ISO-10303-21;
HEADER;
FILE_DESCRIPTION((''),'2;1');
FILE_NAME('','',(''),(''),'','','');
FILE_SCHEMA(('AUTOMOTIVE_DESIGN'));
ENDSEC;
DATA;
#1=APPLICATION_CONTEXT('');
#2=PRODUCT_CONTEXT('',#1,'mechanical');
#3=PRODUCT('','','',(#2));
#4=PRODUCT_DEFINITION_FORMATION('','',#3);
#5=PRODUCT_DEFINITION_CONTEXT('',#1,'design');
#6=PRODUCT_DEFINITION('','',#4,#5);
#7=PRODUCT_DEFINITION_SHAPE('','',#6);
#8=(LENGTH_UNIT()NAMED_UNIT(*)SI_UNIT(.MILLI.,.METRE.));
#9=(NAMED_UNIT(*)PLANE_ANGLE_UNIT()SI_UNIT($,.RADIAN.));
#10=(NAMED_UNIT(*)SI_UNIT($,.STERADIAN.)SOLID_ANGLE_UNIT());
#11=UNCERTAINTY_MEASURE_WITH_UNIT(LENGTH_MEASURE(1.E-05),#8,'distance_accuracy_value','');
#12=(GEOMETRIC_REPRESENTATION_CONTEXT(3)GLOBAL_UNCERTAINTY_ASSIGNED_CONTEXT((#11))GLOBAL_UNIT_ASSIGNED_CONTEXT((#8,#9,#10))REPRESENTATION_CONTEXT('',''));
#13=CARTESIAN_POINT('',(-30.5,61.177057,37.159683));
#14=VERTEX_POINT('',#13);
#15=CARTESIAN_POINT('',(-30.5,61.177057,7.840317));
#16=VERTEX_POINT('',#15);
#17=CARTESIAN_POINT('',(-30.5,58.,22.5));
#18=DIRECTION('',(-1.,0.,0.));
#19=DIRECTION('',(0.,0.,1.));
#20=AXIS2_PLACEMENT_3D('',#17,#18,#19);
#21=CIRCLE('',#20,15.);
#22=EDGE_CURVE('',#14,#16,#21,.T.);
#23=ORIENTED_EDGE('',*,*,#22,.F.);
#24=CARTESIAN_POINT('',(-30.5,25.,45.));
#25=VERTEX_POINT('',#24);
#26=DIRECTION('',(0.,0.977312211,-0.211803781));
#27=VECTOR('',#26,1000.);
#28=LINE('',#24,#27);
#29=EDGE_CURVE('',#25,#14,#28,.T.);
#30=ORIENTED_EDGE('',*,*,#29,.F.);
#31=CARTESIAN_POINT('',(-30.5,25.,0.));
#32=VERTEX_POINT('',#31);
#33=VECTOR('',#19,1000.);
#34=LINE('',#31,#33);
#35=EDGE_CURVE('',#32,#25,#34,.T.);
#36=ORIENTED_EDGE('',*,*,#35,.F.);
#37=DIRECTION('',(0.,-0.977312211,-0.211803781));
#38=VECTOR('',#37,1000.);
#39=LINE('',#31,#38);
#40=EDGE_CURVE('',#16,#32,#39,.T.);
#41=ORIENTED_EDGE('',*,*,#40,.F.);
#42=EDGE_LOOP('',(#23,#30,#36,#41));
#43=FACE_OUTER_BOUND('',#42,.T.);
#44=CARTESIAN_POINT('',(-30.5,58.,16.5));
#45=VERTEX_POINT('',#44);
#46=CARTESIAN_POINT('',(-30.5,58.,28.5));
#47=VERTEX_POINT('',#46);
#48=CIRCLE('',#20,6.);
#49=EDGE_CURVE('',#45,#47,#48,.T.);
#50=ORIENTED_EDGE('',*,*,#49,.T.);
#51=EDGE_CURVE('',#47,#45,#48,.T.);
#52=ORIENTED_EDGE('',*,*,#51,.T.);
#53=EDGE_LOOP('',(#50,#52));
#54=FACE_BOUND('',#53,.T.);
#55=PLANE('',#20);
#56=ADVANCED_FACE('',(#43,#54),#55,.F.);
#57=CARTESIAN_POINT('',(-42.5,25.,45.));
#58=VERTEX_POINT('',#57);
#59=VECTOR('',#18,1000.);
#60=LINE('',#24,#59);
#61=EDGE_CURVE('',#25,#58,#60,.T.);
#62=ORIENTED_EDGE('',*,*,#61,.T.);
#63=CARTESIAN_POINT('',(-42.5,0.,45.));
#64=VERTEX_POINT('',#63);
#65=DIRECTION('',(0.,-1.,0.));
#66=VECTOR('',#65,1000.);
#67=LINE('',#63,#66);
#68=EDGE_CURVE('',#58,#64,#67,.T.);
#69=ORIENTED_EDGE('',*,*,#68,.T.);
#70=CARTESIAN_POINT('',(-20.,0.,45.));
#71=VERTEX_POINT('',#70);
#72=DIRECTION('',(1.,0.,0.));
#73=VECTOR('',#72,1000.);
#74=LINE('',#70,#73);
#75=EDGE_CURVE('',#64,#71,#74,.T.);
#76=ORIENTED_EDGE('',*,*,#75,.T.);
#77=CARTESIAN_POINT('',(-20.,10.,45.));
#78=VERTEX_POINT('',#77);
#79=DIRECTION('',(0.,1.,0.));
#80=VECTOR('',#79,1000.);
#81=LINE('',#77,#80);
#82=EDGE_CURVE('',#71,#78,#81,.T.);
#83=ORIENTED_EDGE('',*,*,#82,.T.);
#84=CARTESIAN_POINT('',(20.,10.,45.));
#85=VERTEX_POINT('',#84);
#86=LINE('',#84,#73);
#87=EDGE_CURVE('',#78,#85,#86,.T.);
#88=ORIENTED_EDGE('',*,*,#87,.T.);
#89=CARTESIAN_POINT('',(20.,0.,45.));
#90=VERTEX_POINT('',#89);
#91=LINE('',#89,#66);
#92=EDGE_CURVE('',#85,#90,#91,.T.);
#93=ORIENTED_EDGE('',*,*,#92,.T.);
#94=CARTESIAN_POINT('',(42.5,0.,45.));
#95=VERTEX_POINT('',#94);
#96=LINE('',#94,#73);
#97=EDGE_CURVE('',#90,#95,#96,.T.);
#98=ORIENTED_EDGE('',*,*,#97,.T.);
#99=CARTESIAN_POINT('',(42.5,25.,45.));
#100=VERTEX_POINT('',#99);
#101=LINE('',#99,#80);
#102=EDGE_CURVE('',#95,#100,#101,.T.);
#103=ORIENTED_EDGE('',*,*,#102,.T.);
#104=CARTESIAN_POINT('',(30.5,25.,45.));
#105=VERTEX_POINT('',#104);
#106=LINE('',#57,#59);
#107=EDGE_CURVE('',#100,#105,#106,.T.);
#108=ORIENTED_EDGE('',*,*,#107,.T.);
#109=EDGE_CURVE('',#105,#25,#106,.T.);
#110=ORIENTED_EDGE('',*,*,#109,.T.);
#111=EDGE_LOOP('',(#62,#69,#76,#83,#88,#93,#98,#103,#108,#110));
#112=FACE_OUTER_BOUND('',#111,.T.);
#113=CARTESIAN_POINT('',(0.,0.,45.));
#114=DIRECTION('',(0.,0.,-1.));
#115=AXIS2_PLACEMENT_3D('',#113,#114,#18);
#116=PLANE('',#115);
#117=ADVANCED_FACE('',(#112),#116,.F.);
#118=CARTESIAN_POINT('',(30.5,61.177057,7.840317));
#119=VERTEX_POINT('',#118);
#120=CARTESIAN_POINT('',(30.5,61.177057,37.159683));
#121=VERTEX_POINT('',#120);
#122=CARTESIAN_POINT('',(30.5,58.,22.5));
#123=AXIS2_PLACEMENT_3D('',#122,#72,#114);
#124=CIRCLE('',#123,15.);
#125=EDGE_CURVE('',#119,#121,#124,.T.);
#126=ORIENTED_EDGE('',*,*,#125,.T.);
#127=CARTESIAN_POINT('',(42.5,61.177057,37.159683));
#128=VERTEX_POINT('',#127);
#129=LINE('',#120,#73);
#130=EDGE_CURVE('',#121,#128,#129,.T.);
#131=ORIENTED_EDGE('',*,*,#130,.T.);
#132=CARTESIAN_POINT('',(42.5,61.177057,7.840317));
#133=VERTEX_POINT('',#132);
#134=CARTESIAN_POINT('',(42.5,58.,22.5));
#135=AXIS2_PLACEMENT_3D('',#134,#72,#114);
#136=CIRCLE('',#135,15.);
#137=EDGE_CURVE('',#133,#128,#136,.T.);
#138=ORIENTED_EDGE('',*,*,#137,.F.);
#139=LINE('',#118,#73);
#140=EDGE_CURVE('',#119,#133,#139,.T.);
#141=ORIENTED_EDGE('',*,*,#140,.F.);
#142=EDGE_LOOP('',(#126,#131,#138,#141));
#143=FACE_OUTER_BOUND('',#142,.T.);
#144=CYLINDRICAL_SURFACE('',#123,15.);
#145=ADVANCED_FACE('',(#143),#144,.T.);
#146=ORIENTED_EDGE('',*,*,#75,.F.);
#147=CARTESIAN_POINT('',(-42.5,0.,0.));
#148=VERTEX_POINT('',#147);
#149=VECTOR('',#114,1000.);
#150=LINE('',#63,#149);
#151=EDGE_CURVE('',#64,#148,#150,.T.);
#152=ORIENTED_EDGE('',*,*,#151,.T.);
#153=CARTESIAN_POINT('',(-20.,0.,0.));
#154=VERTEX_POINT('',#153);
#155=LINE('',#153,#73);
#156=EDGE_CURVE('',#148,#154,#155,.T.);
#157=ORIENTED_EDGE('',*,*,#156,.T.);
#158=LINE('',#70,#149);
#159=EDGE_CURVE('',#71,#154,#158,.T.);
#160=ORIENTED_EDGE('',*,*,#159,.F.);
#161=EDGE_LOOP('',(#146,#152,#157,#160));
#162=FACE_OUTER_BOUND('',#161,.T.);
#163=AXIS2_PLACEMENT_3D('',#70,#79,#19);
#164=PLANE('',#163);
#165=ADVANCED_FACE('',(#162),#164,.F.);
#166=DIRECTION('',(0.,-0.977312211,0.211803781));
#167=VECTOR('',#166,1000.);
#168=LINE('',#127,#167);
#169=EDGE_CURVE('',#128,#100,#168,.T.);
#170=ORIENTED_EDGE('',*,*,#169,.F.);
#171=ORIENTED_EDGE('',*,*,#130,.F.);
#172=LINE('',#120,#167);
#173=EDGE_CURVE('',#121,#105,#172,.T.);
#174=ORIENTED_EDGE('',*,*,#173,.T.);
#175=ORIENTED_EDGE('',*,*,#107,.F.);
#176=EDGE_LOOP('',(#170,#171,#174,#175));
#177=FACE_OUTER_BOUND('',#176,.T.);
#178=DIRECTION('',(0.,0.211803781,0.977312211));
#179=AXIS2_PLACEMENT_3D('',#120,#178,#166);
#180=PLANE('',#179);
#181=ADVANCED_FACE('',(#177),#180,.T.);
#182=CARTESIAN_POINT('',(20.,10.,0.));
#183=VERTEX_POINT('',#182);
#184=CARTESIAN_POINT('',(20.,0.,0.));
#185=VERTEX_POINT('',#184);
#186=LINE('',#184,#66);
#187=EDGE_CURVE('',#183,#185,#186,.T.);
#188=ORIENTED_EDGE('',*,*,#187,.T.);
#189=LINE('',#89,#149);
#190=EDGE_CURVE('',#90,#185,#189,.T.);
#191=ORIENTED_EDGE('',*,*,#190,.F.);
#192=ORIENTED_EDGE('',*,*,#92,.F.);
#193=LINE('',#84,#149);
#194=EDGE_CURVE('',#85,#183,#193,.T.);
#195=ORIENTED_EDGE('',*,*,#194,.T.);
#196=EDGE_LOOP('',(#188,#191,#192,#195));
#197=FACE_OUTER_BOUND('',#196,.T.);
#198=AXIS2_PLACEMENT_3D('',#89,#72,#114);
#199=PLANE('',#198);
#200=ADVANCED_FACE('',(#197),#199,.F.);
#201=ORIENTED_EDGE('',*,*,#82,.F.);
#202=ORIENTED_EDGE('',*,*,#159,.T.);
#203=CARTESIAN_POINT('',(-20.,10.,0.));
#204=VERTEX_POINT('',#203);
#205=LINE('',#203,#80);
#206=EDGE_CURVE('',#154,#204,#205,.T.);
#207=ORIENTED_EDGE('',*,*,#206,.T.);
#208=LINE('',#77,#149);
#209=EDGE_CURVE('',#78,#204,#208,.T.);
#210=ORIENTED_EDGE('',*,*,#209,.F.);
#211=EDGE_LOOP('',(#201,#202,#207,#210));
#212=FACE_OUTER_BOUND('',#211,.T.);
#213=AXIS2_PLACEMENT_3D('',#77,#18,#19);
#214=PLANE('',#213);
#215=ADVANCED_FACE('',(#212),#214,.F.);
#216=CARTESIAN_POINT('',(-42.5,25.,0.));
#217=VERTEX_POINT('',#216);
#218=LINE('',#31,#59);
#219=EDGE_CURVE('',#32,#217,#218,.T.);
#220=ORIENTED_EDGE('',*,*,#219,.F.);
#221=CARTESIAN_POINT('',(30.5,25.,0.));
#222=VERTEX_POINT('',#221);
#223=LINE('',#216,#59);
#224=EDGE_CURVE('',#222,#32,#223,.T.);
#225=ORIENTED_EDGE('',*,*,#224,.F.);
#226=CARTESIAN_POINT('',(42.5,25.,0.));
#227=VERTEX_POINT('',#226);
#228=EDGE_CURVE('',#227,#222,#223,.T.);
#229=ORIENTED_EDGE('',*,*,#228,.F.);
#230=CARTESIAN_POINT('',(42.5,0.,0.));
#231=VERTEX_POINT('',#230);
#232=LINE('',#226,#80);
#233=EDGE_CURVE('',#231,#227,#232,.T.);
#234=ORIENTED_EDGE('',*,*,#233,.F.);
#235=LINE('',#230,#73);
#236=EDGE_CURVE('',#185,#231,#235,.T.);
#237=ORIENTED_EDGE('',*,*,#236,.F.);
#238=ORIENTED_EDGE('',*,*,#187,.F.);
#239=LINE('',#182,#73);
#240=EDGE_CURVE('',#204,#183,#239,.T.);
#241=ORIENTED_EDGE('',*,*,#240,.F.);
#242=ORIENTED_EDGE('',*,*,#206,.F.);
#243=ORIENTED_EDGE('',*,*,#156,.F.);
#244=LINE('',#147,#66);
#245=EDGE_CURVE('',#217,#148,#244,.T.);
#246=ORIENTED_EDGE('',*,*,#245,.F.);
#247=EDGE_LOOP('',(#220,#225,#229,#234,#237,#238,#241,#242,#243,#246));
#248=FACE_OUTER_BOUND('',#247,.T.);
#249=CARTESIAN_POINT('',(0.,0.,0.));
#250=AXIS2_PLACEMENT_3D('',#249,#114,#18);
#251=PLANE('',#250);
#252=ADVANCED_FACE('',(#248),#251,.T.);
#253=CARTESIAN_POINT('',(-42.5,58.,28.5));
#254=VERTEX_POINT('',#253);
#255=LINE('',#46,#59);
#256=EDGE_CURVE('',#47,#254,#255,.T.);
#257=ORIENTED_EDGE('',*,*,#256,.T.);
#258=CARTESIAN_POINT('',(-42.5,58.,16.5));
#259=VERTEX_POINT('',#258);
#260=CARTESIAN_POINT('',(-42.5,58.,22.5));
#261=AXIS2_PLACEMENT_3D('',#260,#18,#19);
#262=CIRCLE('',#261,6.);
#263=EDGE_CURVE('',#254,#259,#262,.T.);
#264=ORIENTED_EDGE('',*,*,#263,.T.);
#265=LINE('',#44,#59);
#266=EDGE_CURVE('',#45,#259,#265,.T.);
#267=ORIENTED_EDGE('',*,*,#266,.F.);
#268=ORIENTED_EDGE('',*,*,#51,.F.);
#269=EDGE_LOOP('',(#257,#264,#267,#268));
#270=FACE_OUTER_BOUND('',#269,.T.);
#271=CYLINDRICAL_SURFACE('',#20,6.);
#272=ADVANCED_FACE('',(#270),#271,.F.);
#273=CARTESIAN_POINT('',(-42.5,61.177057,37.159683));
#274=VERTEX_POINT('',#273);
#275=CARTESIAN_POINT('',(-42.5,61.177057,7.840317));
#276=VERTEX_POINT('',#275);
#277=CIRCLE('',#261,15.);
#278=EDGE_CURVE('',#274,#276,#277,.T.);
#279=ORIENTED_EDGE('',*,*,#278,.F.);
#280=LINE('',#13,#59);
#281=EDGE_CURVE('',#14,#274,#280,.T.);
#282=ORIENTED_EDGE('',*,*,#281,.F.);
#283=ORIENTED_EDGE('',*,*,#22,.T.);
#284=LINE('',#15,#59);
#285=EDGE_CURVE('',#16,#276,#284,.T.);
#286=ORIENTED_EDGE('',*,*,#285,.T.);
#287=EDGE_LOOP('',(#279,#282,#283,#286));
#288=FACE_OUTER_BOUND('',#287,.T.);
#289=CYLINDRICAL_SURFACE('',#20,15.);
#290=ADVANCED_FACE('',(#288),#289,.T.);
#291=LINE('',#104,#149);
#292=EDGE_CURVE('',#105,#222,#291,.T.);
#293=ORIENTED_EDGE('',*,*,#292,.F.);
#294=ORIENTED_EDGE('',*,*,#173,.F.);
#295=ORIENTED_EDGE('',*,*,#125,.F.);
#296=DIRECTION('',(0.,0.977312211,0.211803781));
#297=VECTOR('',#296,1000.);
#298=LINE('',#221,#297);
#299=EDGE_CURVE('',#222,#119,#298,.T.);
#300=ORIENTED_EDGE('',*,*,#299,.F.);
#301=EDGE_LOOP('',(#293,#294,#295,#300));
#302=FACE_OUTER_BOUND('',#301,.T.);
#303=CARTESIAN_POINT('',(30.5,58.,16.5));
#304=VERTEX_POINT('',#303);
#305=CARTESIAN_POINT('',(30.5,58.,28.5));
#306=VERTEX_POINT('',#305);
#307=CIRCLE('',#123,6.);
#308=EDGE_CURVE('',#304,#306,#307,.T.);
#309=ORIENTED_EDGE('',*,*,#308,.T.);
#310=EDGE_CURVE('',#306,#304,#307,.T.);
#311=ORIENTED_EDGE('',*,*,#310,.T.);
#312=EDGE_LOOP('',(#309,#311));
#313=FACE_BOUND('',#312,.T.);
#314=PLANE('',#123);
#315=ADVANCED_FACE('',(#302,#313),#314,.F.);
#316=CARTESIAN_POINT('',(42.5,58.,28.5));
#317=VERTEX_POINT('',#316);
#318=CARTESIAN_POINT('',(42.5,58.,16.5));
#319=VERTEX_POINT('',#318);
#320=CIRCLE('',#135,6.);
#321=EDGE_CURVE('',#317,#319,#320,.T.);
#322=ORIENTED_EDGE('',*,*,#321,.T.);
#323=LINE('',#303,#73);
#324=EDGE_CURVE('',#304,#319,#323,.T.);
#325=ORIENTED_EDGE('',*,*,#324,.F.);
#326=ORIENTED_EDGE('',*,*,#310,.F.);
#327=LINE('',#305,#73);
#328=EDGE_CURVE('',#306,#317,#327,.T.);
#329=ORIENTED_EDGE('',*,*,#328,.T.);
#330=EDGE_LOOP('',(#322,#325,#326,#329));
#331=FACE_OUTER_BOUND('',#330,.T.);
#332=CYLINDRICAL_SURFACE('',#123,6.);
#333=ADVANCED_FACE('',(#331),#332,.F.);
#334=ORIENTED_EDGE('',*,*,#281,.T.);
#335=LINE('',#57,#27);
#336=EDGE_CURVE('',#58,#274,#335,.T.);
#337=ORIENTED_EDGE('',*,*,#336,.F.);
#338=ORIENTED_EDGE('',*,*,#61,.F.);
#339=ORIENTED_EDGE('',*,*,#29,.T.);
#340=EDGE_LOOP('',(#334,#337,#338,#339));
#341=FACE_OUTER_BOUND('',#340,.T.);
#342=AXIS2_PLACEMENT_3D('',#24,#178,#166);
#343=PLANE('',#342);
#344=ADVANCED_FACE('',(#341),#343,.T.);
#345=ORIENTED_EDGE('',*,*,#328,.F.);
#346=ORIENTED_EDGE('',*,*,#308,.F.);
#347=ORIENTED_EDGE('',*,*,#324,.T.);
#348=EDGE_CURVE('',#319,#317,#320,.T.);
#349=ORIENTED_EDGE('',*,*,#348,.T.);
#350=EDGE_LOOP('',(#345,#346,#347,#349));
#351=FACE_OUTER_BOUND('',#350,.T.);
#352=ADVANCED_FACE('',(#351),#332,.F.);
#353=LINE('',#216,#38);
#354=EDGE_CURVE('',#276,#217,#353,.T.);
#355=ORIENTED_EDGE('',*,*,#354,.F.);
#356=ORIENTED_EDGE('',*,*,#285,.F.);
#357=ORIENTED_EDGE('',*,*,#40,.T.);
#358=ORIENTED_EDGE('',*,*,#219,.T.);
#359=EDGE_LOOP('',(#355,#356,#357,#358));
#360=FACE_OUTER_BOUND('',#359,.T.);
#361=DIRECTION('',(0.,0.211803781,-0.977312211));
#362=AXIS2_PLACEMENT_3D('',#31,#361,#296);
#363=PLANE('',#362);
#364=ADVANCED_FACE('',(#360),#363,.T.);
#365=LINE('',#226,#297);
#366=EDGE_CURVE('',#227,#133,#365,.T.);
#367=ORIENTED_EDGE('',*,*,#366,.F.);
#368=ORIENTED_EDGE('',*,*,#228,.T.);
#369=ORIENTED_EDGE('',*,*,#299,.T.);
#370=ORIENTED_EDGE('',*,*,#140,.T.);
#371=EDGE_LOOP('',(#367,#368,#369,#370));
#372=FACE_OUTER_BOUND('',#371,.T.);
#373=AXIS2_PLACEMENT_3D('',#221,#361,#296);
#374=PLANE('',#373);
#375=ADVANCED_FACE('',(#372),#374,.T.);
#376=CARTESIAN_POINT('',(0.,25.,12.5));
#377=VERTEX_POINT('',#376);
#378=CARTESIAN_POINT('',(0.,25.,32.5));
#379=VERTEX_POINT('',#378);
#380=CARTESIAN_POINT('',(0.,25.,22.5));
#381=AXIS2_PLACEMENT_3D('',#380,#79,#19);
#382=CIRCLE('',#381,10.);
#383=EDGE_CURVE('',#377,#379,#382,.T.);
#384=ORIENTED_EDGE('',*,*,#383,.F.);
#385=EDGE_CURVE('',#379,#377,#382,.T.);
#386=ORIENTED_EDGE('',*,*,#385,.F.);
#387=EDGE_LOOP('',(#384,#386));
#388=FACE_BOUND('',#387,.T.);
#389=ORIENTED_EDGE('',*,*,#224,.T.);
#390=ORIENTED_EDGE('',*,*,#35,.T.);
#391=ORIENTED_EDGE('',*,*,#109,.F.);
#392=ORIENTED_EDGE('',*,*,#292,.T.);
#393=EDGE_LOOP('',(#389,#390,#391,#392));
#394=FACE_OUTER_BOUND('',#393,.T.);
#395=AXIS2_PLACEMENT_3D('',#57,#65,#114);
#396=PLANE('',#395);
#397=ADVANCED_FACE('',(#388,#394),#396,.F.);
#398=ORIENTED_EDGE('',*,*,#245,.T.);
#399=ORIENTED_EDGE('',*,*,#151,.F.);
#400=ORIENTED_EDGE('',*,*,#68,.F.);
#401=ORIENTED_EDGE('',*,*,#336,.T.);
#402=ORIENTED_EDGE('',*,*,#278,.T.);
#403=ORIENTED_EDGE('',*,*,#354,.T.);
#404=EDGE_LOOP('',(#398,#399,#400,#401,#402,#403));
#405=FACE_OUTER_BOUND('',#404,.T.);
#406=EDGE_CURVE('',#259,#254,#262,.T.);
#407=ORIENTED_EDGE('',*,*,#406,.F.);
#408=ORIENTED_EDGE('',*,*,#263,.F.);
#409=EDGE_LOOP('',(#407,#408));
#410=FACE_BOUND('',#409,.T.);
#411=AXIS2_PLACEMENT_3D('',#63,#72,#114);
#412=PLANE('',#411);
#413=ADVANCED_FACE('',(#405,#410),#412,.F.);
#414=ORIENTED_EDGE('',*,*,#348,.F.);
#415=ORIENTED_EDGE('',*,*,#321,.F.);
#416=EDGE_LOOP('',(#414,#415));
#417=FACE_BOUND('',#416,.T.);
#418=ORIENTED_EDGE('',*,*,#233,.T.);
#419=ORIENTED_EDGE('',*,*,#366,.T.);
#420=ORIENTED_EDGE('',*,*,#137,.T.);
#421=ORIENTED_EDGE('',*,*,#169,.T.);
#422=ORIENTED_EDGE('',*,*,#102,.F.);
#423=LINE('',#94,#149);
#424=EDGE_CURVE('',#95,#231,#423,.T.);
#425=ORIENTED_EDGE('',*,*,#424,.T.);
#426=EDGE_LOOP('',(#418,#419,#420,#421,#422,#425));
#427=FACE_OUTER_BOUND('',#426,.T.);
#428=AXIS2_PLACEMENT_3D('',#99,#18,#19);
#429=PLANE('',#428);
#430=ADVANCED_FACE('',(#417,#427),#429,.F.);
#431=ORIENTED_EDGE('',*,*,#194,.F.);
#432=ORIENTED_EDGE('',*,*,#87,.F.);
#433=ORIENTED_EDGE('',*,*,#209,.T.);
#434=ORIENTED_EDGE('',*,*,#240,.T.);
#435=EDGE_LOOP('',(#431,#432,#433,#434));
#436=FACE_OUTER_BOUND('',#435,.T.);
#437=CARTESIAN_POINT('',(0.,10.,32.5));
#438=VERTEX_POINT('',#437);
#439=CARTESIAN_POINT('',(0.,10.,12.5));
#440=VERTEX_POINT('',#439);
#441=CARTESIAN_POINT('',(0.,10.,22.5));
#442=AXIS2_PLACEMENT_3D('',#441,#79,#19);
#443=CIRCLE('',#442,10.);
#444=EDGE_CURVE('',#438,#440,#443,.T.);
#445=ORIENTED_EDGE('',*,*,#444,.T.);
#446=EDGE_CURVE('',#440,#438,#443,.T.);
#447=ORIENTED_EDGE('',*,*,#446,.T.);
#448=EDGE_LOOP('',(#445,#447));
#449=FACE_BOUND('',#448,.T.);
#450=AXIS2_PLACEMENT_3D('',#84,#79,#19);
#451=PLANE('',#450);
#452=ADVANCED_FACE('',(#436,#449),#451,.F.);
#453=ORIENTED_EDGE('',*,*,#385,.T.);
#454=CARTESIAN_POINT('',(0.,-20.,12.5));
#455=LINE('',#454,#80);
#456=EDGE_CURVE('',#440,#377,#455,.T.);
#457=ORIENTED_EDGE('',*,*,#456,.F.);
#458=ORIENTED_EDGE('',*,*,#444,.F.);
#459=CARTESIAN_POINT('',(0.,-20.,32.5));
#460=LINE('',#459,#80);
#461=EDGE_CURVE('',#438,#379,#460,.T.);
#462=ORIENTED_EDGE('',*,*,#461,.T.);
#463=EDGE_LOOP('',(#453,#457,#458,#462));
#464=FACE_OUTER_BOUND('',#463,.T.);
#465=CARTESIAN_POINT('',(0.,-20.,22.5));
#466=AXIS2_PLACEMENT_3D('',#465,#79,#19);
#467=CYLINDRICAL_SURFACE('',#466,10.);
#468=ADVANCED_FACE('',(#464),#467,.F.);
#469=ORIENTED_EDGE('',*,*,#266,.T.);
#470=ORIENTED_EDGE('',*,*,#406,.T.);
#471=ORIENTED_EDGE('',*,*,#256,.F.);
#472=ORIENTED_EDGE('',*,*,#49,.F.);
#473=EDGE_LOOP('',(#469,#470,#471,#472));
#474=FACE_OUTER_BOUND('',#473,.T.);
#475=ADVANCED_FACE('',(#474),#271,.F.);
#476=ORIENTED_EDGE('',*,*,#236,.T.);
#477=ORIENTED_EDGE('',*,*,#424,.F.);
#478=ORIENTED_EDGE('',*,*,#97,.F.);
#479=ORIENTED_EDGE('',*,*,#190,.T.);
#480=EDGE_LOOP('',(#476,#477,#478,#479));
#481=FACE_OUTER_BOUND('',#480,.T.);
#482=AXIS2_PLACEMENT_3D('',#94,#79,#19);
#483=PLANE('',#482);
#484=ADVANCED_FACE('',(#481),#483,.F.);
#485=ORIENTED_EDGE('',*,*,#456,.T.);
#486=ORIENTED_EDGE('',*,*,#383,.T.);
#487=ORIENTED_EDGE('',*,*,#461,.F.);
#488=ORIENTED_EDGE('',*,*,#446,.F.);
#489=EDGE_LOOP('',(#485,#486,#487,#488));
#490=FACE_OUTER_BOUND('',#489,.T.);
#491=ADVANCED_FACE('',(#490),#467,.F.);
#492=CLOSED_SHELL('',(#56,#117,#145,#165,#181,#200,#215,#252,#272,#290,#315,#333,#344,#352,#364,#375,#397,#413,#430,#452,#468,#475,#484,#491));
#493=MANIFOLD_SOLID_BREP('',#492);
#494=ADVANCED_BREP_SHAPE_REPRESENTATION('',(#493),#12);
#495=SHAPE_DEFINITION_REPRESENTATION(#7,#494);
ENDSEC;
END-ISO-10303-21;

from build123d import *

# Parameters (mm, degrees)
T_SLOT_BASE_DEPTH      = 45
CENTRE_BORE_SKETCH_R   = 10
CENTRE_BORE_20_DEPTH   = 45
CLEVIS_LUG_1_PROFILE_R = 6
CLEVIS_LUG_1_DEPTH     = 12
CLEVIS_START           = -12
CLEVIS_LUG_2_PROFILE_R = 6
CLEVIS_LUG_2_DEPTH     = 12


with BuildPart() as part:
    # T-Slot Base Profile → T-Slot Base (new body)
    with BuildSketch(Plane.XY):
        Polygon((-20, 0), (-42.5, 0), (-42.5, 25), (42.5, 25), (42.5, 0), (20, 0), (20, 10), (-20, 10), align=None)
    extrude(amount=T_SLOT_BASE_DEPTH)

    # Centre Bore Sketch → Centre Bore Ø20 (cut)
    with BuildSketch(Plane(origin=(0, 25, 0), x_dir=(1, 0, 0), z_dir=(0, 1, 0))):
        with Locations(Location((0, -22.5, 0), (0, 0, 270))):
            Circle(CENTRE_BORE_SKETCH_R)
    extrude(amount=-CENTRE_BORE_20_DEPTH, mode=Mode.SUBTRACT)

    # Clevis Lug 1 Profile → Clevis Lug 1 (add)
    with BuildSketch(Plane.ZY.offset(42.5)):
        with BuildLine():
            Line((0, 25), (45, 25))
            Line((45, 25), (37.159683171, 61.177056708))
            ThreePointArc((37.159683171, 61.177056708), (22.5, 73), (7.840316829, 61.177056708))
            Line((7.840316829, 61.177056708), (0, 25))
        make_face()
        with Locations((22.5, 58)):
            Circle(CLEVIS_LUG_1_PROFILE_R, mode=Mode.SUBTRACT)
    extrude(amount=-CLEVIS_LUG_1_DEPTH)

    # Clevis Lug 2 Profile → Clevis Lug 2 (add)
    with BuildSketch(Plane(origin=(42.5, 0, 0), x_dir=(0, 0, -1), z_dir=(1, 0, 0)).offset(CLEVIS_START)):
        with BuildLine():
            Line((-37.159683171, 61.177056708), (-45, 25))
            Line((-45, 25), (0, 25))
            Line((0, 25), (-7.840316829, 61.177056708))
            ThreePointArc((-7.840316829, 61.177056708), (-22.5, 73), (-37.159683171, 61.177056708))
        make_face()
        with Locations(Location((-22.5, 58, 0), (0, 0, 180))):
            Circle(CLEVIS_LUG_2_PROFILE_R, mode=Mode.SUBTRACT)
    extrude(amount=CLEVIS_LUG_2_DEPTH)


solid = part.part
